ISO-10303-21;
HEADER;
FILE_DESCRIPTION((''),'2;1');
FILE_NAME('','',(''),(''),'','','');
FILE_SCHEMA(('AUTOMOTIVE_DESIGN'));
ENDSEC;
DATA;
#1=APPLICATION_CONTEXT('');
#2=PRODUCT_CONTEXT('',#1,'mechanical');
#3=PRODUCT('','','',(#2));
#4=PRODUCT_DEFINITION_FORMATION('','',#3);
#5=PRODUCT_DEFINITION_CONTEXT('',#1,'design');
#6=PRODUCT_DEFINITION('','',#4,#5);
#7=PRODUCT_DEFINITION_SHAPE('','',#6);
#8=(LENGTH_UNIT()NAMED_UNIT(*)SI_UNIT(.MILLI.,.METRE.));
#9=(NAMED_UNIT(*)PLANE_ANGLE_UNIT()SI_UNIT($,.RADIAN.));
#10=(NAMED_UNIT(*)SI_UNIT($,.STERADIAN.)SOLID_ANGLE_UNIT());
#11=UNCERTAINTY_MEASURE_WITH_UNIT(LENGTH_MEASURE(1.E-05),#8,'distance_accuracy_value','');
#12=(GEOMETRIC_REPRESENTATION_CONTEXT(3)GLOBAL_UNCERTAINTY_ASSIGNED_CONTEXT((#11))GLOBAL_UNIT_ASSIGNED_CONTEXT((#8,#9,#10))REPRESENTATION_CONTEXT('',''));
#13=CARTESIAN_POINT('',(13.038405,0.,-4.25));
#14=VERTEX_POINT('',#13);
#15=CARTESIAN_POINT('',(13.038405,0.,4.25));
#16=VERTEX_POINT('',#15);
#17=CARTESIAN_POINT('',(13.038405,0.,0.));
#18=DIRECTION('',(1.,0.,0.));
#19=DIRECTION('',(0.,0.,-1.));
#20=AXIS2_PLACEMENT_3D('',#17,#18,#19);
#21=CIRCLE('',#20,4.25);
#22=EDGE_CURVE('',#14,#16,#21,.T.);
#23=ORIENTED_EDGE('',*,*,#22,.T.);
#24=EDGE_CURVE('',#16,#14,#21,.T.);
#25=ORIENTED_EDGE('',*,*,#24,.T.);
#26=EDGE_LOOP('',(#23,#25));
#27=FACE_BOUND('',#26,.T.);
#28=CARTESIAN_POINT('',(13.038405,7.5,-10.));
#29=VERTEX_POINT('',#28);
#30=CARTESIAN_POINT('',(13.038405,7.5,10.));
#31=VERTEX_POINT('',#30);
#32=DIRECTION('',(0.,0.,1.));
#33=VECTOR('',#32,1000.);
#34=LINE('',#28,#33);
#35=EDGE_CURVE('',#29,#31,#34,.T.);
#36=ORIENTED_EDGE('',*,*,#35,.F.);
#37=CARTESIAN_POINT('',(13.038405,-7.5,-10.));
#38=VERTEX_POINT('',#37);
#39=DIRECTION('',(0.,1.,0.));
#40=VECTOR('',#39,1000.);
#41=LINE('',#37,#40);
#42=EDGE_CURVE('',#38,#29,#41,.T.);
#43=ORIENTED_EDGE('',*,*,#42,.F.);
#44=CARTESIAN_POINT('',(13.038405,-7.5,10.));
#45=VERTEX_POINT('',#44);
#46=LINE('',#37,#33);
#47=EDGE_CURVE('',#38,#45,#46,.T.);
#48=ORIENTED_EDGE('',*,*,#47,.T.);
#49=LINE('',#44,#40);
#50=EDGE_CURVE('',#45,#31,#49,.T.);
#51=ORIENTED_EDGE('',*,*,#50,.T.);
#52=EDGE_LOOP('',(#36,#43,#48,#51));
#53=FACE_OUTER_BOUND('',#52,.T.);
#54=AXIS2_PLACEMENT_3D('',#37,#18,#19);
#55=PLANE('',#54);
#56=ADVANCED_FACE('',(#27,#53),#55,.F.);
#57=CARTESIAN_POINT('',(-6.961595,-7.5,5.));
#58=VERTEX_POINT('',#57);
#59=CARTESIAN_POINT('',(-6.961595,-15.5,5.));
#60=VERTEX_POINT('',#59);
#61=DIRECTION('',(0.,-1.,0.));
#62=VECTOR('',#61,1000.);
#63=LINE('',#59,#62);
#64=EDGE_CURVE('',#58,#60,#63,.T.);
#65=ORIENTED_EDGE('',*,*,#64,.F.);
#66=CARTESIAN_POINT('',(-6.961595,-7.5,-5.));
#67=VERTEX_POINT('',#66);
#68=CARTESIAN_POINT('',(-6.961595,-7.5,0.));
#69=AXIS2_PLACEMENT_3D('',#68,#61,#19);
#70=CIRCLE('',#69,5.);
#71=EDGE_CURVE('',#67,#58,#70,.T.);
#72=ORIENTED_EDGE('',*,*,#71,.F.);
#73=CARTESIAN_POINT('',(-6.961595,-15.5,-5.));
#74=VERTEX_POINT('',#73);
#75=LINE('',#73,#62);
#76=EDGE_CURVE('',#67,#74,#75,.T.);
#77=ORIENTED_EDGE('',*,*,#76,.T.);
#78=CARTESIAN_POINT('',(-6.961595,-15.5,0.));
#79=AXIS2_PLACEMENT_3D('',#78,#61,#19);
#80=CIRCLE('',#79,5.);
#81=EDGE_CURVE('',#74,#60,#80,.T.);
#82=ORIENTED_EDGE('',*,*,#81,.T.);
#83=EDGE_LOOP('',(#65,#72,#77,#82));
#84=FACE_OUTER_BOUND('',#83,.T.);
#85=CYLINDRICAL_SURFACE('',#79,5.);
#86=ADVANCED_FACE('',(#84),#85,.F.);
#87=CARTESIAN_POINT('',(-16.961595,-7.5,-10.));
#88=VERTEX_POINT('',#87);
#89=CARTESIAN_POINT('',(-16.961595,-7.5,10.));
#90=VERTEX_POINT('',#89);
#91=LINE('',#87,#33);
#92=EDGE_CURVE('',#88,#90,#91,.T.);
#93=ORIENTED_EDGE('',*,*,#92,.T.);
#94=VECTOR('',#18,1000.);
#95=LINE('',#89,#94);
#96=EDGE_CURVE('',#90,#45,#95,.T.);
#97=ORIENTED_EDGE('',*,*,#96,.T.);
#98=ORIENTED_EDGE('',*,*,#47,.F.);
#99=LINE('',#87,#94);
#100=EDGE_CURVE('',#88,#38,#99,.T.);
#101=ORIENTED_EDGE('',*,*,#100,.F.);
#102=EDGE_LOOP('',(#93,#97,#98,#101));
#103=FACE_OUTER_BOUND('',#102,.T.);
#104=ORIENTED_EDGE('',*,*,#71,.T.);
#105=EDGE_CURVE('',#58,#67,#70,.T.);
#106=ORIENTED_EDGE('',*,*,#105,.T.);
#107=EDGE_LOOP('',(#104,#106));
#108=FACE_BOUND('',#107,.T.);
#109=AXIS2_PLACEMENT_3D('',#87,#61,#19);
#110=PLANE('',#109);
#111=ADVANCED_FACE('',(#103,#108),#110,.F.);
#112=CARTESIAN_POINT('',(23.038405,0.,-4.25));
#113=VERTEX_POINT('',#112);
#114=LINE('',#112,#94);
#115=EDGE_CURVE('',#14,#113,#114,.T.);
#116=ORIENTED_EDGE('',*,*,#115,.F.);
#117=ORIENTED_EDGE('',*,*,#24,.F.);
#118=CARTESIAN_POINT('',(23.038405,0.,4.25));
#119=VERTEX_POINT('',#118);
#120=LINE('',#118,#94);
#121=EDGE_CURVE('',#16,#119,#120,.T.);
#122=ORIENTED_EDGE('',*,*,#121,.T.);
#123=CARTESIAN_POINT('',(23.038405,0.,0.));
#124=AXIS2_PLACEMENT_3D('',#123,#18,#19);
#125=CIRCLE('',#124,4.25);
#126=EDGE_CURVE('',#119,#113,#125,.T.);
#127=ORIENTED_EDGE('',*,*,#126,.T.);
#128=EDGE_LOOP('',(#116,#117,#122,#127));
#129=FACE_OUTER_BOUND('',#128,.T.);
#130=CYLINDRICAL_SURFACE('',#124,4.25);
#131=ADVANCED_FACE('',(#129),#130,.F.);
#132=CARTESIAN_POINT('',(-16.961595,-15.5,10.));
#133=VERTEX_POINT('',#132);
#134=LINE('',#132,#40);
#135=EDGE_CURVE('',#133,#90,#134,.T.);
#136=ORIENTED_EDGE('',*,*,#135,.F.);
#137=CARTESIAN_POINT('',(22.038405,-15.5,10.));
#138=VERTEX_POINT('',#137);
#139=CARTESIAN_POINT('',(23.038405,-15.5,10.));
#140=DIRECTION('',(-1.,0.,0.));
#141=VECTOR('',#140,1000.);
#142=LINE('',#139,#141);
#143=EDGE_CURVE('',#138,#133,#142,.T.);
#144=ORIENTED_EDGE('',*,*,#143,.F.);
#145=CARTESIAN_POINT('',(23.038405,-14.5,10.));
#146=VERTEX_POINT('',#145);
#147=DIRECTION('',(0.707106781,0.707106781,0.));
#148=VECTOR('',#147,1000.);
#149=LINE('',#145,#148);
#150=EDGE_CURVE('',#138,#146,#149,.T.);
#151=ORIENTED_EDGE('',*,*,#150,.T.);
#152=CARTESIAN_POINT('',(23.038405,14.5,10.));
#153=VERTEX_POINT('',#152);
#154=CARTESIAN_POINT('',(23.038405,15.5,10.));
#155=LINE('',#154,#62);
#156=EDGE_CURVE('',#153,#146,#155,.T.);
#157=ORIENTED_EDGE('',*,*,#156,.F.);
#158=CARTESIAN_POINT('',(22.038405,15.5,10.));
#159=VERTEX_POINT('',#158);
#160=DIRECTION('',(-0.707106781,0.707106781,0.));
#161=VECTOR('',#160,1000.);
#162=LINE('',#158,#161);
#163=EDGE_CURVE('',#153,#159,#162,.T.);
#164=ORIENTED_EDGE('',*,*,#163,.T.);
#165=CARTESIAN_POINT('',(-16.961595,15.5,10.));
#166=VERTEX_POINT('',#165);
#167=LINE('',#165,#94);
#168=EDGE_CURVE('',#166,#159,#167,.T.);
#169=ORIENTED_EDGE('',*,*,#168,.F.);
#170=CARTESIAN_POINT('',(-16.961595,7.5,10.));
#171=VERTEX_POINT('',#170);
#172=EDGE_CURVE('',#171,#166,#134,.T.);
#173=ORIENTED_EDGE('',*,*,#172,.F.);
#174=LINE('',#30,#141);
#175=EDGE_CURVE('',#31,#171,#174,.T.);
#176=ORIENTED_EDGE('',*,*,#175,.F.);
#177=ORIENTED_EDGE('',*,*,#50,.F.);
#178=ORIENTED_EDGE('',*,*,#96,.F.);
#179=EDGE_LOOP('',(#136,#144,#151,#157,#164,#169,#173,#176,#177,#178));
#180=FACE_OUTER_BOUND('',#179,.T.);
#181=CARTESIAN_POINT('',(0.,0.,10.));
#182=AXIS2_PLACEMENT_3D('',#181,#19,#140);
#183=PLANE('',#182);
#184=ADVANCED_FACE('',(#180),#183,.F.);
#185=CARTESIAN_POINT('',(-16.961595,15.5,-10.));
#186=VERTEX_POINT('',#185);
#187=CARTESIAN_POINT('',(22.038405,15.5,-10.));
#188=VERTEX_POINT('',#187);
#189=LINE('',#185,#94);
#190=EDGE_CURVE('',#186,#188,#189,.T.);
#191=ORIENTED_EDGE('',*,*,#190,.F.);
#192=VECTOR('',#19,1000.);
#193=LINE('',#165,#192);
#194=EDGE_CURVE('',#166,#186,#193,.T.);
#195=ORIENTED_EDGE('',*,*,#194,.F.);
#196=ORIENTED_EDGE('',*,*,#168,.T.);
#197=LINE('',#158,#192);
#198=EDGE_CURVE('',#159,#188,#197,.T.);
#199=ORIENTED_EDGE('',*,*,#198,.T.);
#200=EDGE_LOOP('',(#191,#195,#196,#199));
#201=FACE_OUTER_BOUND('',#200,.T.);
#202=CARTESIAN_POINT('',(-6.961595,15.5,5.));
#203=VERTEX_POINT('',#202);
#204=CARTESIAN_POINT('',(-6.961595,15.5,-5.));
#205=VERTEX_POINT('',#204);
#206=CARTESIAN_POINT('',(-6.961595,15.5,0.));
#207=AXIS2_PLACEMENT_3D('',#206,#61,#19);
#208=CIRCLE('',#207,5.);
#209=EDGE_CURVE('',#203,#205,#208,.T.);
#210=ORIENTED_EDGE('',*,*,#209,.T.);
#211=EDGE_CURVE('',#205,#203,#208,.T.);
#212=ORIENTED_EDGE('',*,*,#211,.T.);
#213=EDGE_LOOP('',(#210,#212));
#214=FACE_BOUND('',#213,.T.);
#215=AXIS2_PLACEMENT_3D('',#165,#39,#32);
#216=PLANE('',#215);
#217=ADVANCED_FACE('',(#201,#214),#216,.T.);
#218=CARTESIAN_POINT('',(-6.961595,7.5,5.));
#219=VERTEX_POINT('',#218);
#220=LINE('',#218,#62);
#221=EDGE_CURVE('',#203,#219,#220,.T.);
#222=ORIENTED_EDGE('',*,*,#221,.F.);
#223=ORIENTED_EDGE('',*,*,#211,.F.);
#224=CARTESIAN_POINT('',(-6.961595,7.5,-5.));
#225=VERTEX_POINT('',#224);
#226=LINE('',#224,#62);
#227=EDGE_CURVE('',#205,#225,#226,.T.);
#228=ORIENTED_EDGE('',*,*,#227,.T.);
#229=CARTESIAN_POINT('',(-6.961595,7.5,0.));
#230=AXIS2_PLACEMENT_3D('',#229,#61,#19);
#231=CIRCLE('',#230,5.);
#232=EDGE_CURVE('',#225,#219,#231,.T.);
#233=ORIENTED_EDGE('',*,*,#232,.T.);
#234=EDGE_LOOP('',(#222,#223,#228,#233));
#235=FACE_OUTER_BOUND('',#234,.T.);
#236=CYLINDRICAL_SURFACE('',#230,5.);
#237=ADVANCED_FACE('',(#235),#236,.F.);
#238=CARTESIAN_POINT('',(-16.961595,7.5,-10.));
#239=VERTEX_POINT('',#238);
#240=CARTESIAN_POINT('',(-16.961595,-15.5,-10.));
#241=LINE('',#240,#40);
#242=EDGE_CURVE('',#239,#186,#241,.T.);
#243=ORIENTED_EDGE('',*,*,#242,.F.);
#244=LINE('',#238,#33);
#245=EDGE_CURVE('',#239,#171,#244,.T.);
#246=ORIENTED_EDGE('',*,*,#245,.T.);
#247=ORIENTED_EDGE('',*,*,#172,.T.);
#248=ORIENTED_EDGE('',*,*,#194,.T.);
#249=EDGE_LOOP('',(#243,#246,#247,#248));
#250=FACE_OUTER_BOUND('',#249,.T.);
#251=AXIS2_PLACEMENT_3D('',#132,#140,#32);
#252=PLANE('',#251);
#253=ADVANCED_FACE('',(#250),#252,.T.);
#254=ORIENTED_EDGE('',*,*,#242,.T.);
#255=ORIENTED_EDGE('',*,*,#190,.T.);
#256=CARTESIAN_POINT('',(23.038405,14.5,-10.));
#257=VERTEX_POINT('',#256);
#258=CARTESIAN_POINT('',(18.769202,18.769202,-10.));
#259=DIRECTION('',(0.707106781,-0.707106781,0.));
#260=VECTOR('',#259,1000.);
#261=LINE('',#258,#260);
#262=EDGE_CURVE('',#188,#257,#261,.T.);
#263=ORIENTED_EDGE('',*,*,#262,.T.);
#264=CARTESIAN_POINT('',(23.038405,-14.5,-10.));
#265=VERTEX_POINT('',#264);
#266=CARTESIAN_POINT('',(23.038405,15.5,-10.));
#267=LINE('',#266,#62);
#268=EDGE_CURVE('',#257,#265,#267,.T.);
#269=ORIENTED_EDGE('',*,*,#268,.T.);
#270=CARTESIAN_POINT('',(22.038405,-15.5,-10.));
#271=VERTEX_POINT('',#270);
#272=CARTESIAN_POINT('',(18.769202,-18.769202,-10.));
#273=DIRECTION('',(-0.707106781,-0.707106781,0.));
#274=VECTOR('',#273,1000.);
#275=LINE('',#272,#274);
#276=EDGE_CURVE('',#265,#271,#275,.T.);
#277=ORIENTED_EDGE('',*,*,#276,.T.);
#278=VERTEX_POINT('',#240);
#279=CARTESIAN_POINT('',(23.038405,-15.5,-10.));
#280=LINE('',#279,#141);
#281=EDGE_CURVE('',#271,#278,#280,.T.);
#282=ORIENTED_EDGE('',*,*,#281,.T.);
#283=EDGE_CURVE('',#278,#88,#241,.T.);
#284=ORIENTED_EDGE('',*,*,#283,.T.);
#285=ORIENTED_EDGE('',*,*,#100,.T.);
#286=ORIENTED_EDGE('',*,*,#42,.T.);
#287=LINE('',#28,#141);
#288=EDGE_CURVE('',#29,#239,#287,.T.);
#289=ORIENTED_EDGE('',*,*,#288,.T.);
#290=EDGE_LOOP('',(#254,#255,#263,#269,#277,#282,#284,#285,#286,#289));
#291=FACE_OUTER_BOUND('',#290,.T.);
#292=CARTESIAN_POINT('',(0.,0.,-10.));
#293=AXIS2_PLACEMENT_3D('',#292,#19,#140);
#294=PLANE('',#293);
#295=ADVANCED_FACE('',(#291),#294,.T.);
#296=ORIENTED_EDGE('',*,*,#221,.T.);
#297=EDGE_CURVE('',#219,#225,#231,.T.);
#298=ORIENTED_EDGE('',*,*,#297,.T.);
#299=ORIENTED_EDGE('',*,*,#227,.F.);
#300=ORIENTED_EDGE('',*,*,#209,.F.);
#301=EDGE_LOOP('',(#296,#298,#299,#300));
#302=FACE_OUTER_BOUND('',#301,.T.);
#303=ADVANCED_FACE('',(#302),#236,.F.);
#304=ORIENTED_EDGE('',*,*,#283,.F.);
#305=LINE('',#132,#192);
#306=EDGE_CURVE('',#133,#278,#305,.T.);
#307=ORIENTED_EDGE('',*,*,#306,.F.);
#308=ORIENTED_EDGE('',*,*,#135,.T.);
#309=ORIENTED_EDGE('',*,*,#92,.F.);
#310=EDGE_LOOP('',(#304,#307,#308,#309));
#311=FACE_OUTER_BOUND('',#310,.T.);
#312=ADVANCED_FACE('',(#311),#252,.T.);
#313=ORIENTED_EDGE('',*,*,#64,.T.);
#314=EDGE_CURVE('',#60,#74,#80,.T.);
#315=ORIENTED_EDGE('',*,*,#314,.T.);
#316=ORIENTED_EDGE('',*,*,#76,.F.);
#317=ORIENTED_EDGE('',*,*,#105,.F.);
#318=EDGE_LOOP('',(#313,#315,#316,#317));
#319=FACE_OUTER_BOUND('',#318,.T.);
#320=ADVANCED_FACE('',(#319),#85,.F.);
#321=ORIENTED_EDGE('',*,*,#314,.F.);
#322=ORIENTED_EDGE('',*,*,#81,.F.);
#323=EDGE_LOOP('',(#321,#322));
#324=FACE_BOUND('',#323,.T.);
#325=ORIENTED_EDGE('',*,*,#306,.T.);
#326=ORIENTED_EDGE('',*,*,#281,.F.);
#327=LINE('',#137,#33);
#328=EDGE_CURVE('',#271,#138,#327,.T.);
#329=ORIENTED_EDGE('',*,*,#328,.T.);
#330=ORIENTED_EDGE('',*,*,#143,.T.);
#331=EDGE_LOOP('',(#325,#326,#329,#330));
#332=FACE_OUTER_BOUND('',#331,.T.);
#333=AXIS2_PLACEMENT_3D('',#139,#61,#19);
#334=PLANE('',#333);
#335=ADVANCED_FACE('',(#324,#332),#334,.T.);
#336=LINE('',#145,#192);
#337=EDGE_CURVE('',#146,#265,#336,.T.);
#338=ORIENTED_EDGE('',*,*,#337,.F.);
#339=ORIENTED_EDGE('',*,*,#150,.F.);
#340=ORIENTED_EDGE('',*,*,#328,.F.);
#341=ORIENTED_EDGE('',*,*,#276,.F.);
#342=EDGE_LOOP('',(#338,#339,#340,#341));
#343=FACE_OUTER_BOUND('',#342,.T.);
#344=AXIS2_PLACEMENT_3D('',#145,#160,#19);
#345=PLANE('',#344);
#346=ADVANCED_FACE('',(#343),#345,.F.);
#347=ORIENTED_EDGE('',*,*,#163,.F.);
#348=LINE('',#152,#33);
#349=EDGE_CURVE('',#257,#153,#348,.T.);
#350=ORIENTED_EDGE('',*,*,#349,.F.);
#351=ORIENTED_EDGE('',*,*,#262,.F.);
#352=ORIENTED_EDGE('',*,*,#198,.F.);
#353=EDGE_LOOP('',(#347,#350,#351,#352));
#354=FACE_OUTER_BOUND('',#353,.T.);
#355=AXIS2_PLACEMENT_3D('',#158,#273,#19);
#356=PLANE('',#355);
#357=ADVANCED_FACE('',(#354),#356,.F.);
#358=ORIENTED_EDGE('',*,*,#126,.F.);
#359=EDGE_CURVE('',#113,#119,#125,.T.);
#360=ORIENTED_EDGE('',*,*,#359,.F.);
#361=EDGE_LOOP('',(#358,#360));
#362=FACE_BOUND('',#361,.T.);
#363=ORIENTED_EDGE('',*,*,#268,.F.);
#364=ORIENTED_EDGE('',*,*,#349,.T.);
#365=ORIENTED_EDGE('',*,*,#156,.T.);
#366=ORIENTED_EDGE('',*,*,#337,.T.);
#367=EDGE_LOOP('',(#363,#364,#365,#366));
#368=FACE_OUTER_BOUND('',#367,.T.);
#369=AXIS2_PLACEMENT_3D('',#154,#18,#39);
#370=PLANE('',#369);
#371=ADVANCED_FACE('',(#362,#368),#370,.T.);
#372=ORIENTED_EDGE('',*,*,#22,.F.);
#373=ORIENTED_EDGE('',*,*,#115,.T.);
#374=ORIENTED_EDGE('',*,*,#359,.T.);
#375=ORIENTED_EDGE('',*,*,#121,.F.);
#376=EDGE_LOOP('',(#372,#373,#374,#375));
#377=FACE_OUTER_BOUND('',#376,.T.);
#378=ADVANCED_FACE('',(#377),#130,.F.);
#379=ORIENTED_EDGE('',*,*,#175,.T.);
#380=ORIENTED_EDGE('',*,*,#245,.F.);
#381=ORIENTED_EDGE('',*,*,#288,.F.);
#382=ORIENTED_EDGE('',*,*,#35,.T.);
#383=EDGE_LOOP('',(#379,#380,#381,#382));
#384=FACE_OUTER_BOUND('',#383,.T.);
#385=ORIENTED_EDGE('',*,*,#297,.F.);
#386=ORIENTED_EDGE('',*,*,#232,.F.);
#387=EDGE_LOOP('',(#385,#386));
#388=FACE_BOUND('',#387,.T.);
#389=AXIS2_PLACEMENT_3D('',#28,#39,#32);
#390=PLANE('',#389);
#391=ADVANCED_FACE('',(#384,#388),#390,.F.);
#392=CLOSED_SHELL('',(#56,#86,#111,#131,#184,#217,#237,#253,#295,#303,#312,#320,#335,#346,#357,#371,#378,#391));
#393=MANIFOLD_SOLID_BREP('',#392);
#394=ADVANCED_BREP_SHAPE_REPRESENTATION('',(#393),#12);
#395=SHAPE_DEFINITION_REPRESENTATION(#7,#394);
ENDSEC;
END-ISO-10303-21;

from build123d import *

# Parameters (mm, degrees)
SKETCH_1_W                  = 40
SKETCH_1_H                  = 31
EXTRUDE_1_DEPTH             = 20
SKETCH_2_W                  = 30
SKETCH_2_H                  = 15
CUT_EXTRUDE_1_DEPTH         = 35.220141674
HOLE_WIZARD_10_0_10_1_D     = 10
HOLE_WIZARD_10_0_10_1_DEPTH = 8
HOLE_WIZARD_8_5_8_5_1_D     = 8.5
HOLE_WIZARD_8_5_8_5_1_DEPTH = 40
HOLE_WIZARD_10_0_10_2_D     = 10
CHAMFER_1_SIZE              = 1


with BuildPart() as part:
    # 草图1 → 凸台-拉伸1 (new body)
    with BuildSketch(Plane(origin=(0, 0, -10), x_dir=(-1, 0, 0), z_dir=(0, 0, -1))):
        with Locations((-3.03840481, 0)):
            Rectangle(SKETCH_1_W, SKETCH_1_H)
    extrude(amount=-EXTRUDE_1_DEPTH)

    # 草图2 → 切除-拉伸1 (cut, through all)
    with BuildSketch(Plane.XY.offset(10)):
        with Locations((-1.96159519, 0)):
            Rectangle(SKETCH_2_W, SKETCH_2_H)
    extrude(amount=-CUT_EXTRUDE_1_DEPTH, mode=Mode.SUBTRACT)

    # Ø10.0 (10) 直径孔1
    with Locations(Plane(origin=(0, -15.5, 0), x_dir=(-1, 0, 0), z_dir=(0, -1, 0))):
        with Locations((6.96159519, 0)):
            Hole(HOLE_WIZARD_10_0_10_1_D / 2, depth=HOLE_WIZARD_10_0_10_1_DEPTH)

    # Ø8.5 (8.5) 直径孔1
    with Locations(Plane(origin=(23.03840481, 0, 0), x_dir=(0, 0, -1), z_dir=(1, 0, 0))):
        with Locations((0, 0)):
            Hole(HOLE_WIZARD_8_5_8_5_1_D / 2, depth=HOLE_WIZARD_8_5_8_5_1_DEPTH)

    # Ø10.0 (10) 直径孔2 (through all)
    with Locations(Plane(origin=(0, 7.5, 0), x_dir=(-1, 0, 0), z_dir=(0, -1, 0))):
        with Locations((6.96159519, 0)):
            Hole(HOLE_WIZARD_10_0_10_2_D / 2)

    # 倒角1
    chamfer_1_edges = [part.edges().sort_by_distance(p)[0] for p in [
        (23.03840481, -15.5, 0),
        (23.03840481, 15.5, 0),
    ]]
    chamfer(chamfer_1_edges, length=CHAMFER_1_SIZE)


solid = part.part
